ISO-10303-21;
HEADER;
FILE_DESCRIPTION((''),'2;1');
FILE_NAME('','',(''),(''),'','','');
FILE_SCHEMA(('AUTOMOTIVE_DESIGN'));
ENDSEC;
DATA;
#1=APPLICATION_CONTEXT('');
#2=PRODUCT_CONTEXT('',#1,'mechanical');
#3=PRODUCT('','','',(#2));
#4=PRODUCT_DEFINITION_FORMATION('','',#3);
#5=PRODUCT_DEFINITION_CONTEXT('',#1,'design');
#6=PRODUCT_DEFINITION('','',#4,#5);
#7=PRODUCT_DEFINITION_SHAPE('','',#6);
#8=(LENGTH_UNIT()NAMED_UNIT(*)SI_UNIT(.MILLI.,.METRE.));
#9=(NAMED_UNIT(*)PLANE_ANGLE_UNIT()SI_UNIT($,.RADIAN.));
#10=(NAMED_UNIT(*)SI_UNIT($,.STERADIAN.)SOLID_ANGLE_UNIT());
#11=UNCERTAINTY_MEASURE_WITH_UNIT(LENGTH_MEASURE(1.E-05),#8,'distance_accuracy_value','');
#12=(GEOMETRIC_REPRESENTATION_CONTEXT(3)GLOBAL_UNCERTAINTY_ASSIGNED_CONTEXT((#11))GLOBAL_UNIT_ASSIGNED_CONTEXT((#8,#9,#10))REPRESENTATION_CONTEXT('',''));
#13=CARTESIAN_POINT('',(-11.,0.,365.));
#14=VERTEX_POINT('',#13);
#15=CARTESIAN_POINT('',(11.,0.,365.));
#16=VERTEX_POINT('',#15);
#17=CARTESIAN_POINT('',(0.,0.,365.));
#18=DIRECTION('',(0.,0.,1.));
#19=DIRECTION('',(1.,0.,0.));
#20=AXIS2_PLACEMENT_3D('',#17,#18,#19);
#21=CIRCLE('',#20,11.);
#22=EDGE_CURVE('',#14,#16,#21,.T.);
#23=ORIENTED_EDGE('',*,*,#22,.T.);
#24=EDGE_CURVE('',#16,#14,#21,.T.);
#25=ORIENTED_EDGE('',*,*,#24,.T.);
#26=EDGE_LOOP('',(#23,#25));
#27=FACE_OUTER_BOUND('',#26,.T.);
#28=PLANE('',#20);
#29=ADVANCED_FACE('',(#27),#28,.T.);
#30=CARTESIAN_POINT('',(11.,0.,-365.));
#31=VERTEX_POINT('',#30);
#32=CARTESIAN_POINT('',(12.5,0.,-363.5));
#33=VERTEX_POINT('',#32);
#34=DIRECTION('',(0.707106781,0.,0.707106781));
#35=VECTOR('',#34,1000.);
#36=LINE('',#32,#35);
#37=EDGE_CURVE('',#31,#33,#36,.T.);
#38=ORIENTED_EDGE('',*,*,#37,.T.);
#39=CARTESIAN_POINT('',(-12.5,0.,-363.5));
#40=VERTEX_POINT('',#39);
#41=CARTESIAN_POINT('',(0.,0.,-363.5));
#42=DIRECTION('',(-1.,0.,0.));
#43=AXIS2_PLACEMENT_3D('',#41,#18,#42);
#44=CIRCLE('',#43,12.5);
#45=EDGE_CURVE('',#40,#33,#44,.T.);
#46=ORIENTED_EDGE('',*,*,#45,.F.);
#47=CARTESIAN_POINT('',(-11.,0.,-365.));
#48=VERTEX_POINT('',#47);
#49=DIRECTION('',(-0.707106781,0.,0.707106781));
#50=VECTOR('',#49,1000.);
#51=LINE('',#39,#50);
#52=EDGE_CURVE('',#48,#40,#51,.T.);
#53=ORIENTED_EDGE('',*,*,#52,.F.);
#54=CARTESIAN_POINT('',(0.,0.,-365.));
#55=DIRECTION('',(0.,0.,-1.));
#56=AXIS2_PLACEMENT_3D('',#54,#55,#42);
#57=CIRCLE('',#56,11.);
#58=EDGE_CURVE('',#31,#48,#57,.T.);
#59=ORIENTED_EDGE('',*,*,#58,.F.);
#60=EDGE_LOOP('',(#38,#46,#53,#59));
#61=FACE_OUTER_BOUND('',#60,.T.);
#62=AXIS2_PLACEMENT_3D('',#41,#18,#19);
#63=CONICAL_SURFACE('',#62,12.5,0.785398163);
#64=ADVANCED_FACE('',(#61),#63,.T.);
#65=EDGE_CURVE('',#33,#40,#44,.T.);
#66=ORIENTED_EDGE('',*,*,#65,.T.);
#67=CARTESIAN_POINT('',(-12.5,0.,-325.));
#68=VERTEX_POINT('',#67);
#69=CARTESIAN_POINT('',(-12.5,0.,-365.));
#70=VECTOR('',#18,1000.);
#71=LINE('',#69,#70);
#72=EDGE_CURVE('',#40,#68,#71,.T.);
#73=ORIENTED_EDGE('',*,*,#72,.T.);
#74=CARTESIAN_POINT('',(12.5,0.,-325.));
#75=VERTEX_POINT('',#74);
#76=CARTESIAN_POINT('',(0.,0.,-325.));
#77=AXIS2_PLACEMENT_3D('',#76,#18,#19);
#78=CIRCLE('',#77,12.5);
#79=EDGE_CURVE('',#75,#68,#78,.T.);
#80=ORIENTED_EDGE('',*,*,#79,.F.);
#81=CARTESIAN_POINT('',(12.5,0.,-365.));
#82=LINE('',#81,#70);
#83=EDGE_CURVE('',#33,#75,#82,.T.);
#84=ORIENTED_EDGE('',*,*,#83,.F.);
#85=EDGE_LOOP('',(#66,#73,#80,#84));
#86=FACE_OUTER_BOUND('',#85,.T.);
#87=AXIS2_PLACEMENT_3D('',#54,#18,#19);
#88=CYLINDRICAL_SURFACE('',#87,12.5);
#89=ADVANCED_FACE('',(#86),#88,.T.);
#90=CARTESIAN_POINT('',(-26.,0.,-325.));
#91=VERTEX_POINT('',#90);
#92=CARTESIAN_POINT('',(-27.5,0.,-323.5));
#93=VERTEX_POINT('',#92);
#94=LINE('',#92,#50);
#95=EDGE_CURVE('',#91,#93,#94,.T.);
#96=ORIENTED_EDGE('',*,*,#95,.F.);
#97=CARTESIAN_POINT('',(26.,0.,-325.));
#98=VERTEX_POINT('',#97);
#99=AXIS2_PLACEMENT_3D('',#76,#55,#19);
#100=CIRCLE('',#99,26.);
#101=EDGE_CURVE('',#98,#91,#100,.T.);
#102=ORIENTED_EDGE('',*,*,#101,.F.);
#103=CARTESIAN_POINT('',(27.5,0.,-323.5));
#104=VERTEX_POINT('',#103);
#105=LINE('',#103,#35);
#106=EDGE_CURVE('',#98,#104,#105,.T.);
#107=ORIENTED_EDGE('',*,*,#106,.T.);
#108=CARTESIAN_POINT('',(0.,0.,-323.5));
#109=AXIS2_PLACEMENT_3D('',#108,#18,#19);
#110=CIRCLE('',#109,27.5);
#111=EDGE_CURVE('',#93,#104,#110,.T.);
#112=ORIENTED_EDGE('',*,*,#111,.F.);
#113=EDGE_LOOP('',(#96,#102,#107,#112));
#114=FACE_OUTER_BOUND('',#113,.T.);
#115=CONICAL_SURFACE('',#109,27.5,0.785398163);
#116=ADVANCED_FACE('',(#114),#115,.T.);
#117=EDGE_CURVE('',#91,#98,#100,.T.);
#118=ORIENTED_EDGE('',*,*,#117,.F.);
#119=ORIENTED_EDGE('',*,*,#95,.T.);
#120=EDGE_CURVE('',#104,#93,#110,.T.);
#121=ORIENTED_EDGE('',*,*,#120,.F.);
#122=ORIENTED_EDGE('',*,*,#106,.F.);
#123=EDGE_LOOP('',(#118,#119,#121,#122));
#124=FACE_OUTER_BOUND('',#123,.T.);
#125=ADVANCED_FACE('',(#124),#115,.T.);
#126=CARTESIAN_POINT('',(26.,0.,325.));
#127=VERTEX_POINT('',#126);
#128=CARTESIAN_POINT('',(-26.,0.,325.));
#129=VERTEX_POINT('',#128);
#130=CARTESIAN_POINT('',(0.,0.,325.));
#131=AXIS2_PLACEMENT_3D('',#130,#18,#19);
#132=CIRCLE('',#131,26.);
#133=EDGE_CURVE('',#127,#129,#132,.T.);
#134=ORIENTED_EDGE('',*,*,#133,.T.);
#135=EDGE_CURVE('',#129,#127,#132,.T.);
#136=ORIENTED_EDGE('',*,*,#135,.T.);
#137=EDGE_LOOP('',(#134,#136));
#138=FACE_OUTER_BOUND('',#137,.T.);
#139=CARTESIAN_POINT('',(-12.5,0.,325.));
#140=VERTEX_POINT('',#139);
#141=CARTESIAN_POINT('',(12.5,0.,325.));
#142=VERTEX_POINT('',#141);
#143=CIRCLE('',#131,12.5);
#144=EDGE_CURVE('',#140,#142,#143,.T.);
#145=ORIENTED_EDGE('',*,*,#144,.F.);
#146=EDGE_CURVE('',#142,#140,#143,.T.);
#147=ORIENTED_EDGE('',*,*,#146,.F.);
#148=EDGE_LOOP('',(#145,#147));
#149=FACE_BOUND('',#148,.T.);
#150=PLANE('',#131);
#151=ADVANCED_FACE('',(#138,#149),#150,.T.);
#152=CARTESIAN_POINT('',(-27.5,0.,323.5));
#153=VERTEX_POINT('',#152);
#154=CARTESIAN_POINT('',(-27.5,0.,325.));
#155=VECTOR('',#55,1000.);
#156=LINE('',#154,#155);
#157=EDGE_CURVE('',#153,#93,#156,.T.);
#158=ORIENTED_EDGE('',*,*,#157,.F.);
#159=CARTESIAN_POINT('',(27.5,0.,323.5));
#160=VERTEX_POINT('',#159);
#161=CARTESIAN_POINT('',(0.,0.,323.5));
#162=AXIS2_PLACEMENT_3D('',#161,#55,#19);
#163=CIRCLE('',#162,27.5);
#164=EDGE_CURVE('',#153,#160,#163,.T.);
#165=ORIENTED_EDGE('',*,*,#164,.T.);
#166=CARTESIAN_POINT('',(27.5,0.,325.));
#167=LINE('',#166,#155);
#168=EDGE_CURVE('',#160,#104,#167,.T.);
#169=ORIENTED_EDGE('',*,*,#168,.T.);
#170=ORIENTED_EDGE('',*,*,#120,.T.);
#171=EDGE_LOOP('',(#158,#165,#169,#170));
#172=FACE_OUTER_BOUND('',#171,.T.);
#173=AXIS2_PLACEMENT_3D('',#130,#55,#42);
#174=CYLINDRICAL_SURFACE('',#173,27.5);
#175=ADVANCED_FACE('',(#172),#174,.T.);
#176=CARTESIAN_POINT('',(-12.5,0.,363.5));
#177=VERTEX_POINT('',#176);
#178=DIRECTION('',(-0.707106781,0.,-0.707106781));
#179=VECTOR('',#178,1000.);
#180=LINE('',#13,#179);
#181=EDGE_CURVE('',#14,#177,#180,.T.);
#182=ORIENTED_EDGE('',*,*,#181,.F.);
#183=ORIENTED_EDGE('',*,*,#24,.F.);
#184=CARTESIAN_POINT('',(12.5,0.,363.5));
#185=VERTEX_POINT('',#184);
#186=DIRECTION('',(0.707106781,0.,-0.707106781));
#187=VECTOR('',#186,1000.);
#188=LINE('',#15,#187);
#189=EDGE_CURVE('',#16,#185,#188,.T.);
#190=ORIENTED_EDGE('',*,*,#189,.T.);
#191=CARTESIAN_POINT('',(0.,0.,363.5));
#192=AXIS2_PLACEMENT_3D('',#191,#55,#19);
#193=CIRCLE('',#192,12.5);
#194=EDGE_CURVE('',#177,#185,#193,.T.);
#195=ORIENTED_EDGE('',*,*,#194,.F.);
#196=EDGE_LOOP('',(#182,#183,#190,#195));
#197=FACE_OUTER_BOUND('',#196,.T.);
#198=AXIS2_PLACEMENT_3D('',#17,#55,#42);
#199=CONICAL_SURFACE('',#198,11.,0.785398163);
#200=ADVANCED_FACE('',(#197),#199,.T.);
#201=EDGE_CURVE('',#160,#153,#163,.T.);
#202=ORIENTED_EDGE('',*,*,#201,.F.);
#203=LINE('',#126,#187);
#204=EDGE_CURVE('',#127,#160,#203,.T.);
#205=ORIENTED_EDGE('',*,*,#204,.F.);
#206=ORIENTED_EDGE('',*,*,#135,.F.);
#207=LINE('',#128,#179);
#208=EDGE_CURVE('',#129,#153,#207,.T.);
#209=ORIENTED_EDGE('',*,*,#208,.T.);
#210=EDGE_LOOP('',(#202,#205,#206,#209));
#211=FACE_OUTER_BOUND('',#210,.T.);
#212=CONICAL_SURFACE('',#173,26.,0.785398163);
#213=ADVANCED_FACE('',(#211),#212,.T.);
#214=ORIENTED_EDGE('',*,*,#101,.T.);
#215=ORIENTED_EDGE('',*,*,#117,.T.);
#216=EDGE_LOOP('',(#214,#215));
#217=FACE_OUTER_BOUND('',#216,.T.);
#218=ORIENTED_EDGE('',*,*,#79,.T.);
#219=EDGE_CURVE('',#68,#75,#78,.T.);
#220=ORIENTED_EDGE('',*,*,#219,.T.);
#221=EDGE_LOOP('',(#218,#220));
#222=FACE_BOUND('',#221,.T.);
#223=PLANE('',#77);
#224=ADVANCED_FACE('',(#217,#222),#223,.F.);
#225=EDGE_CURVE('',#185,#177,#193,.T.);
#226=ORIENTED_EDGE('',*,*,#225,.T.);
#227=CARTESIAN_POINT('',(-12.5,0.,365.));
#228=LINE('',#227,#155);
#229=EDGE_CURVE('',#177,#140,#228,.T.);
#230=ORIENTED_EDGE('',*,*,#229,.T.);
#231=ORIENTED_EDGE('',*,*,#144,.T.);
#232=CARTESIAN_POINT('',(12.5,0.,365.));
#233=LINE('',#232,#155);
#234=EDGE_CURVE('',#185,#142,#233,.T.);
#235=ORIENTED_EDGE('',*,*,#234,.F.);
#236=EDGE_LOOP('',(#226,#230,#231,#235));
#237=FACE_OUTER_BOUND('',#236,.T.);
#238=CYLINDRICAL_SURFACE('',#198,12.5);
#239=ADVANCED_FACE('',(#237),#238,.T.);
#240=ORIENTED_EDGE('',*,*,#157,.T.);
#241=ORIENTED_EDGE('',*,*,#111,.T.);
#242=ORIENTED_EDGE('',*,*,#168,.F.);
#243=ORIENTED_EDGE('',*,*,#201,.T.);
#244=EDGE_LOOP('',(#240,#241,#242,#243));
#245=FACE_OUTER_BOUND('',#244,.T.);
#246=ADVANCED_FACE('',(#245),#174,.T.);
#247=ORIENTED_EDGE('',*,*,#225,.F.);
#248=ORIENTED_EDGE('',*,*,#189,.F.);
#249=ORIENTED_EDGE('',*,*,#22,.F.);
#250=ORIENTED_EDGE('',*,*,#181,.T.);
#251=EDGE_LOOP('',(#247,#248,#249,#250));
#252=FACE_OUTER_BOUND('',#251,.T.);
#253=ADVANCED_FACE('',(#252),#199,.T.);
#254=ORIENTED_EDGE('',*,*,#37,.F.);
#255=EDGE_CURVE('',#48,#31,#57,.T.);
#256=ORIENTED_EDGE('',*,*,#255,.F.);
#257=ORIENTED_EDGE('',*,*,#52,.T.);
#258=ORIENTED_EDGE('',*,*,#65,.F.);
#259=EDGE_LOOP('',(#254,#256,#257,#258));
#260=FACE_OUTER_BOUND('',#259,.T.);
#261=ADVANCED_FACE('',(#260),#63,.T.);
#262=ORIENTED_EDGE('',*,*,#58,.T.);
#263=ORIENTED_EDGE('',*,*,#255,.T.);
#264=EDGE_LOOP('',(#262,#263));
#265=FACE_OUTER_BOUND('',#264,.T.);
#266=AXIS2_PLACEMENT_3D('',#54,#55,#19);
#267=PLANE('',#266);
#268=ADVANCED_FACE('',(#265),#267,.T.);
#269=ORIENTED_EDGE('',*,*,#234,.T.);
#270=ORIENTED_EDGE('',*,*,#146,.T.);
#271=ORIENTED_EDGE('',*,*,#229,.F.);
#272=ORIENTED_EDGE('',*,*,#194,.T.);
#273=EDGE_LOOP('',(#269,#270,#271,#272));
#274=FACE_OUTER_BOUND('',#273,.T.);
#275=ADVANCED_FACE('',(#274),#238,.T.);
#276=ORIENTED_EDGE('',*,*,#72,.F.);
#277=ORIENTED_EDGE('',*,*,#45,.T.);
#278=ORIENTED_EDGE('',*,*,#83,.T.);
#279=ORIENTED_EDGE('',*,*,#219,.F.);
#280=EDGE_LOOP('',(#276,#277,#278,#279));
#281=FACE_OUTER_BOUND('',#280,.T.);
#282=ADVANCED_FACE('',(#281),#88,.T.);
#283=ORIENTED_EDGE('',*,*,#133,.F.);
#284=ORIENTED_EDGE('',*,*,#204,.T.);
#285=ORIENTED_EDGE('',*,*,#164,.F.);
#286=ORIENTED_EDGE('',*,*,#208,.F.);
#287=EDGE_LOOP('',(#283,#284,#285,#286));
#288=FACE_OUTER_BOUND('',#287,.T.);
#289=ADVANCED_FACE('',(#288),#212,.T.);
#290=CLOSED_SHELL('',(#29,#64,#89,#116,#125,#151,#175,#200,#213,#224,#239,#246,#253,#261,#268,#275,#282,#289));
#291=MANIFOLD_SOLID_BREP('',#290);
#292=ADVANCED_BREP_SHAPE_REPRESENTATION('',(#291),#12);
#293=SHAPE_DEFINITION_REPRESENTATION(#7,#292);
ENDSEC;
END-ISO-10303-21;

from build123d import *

# Parameters (mm, degrees)
SKETCH1_R           = 27.5
BOSS_EXTRUDE1_DEPTH = 325
SKETCH2_R           = 12.5
BOSS_EXTRUDE2_DEPTH = 40
CHAMFER1_SIZE       = 1.5


with BuildPart() as part:
    # Sketch1 → Boss-Extrude1 (new, symmetric)
    with BuildSketch(Plane.XY):
        Circle(SKETCH1_R)
    extrude(amount=BOSS_EXTRUDE1_DEPTH, both=True)

    # Sketch2 → Boss-Extrude2 (add)
    with BuildSketch(Plane.XY.offset(325)):
        Circle(SKETCH2_R)
    boss_extrude2 = extrude(amount=BOSS_EXTRUDE2_DEPTH)

    # Mirror1: Boss-Extrude2 across plane
    add(boss_extrude2.mirror(Plane.XY))

    # Chamfer1
    chamfer1_edges = [part.edges().sort_by_distance(p)[0] for p in [
        (-12.5, 0, -365),
        (-27.5, 0, -325),
        (-27.5, 0, 325),
        (-12.5, 0, 365),
    ]]
    chamfer(chamfer1_edges, length=CHAMFER1_SIZE)


solid = part.part
